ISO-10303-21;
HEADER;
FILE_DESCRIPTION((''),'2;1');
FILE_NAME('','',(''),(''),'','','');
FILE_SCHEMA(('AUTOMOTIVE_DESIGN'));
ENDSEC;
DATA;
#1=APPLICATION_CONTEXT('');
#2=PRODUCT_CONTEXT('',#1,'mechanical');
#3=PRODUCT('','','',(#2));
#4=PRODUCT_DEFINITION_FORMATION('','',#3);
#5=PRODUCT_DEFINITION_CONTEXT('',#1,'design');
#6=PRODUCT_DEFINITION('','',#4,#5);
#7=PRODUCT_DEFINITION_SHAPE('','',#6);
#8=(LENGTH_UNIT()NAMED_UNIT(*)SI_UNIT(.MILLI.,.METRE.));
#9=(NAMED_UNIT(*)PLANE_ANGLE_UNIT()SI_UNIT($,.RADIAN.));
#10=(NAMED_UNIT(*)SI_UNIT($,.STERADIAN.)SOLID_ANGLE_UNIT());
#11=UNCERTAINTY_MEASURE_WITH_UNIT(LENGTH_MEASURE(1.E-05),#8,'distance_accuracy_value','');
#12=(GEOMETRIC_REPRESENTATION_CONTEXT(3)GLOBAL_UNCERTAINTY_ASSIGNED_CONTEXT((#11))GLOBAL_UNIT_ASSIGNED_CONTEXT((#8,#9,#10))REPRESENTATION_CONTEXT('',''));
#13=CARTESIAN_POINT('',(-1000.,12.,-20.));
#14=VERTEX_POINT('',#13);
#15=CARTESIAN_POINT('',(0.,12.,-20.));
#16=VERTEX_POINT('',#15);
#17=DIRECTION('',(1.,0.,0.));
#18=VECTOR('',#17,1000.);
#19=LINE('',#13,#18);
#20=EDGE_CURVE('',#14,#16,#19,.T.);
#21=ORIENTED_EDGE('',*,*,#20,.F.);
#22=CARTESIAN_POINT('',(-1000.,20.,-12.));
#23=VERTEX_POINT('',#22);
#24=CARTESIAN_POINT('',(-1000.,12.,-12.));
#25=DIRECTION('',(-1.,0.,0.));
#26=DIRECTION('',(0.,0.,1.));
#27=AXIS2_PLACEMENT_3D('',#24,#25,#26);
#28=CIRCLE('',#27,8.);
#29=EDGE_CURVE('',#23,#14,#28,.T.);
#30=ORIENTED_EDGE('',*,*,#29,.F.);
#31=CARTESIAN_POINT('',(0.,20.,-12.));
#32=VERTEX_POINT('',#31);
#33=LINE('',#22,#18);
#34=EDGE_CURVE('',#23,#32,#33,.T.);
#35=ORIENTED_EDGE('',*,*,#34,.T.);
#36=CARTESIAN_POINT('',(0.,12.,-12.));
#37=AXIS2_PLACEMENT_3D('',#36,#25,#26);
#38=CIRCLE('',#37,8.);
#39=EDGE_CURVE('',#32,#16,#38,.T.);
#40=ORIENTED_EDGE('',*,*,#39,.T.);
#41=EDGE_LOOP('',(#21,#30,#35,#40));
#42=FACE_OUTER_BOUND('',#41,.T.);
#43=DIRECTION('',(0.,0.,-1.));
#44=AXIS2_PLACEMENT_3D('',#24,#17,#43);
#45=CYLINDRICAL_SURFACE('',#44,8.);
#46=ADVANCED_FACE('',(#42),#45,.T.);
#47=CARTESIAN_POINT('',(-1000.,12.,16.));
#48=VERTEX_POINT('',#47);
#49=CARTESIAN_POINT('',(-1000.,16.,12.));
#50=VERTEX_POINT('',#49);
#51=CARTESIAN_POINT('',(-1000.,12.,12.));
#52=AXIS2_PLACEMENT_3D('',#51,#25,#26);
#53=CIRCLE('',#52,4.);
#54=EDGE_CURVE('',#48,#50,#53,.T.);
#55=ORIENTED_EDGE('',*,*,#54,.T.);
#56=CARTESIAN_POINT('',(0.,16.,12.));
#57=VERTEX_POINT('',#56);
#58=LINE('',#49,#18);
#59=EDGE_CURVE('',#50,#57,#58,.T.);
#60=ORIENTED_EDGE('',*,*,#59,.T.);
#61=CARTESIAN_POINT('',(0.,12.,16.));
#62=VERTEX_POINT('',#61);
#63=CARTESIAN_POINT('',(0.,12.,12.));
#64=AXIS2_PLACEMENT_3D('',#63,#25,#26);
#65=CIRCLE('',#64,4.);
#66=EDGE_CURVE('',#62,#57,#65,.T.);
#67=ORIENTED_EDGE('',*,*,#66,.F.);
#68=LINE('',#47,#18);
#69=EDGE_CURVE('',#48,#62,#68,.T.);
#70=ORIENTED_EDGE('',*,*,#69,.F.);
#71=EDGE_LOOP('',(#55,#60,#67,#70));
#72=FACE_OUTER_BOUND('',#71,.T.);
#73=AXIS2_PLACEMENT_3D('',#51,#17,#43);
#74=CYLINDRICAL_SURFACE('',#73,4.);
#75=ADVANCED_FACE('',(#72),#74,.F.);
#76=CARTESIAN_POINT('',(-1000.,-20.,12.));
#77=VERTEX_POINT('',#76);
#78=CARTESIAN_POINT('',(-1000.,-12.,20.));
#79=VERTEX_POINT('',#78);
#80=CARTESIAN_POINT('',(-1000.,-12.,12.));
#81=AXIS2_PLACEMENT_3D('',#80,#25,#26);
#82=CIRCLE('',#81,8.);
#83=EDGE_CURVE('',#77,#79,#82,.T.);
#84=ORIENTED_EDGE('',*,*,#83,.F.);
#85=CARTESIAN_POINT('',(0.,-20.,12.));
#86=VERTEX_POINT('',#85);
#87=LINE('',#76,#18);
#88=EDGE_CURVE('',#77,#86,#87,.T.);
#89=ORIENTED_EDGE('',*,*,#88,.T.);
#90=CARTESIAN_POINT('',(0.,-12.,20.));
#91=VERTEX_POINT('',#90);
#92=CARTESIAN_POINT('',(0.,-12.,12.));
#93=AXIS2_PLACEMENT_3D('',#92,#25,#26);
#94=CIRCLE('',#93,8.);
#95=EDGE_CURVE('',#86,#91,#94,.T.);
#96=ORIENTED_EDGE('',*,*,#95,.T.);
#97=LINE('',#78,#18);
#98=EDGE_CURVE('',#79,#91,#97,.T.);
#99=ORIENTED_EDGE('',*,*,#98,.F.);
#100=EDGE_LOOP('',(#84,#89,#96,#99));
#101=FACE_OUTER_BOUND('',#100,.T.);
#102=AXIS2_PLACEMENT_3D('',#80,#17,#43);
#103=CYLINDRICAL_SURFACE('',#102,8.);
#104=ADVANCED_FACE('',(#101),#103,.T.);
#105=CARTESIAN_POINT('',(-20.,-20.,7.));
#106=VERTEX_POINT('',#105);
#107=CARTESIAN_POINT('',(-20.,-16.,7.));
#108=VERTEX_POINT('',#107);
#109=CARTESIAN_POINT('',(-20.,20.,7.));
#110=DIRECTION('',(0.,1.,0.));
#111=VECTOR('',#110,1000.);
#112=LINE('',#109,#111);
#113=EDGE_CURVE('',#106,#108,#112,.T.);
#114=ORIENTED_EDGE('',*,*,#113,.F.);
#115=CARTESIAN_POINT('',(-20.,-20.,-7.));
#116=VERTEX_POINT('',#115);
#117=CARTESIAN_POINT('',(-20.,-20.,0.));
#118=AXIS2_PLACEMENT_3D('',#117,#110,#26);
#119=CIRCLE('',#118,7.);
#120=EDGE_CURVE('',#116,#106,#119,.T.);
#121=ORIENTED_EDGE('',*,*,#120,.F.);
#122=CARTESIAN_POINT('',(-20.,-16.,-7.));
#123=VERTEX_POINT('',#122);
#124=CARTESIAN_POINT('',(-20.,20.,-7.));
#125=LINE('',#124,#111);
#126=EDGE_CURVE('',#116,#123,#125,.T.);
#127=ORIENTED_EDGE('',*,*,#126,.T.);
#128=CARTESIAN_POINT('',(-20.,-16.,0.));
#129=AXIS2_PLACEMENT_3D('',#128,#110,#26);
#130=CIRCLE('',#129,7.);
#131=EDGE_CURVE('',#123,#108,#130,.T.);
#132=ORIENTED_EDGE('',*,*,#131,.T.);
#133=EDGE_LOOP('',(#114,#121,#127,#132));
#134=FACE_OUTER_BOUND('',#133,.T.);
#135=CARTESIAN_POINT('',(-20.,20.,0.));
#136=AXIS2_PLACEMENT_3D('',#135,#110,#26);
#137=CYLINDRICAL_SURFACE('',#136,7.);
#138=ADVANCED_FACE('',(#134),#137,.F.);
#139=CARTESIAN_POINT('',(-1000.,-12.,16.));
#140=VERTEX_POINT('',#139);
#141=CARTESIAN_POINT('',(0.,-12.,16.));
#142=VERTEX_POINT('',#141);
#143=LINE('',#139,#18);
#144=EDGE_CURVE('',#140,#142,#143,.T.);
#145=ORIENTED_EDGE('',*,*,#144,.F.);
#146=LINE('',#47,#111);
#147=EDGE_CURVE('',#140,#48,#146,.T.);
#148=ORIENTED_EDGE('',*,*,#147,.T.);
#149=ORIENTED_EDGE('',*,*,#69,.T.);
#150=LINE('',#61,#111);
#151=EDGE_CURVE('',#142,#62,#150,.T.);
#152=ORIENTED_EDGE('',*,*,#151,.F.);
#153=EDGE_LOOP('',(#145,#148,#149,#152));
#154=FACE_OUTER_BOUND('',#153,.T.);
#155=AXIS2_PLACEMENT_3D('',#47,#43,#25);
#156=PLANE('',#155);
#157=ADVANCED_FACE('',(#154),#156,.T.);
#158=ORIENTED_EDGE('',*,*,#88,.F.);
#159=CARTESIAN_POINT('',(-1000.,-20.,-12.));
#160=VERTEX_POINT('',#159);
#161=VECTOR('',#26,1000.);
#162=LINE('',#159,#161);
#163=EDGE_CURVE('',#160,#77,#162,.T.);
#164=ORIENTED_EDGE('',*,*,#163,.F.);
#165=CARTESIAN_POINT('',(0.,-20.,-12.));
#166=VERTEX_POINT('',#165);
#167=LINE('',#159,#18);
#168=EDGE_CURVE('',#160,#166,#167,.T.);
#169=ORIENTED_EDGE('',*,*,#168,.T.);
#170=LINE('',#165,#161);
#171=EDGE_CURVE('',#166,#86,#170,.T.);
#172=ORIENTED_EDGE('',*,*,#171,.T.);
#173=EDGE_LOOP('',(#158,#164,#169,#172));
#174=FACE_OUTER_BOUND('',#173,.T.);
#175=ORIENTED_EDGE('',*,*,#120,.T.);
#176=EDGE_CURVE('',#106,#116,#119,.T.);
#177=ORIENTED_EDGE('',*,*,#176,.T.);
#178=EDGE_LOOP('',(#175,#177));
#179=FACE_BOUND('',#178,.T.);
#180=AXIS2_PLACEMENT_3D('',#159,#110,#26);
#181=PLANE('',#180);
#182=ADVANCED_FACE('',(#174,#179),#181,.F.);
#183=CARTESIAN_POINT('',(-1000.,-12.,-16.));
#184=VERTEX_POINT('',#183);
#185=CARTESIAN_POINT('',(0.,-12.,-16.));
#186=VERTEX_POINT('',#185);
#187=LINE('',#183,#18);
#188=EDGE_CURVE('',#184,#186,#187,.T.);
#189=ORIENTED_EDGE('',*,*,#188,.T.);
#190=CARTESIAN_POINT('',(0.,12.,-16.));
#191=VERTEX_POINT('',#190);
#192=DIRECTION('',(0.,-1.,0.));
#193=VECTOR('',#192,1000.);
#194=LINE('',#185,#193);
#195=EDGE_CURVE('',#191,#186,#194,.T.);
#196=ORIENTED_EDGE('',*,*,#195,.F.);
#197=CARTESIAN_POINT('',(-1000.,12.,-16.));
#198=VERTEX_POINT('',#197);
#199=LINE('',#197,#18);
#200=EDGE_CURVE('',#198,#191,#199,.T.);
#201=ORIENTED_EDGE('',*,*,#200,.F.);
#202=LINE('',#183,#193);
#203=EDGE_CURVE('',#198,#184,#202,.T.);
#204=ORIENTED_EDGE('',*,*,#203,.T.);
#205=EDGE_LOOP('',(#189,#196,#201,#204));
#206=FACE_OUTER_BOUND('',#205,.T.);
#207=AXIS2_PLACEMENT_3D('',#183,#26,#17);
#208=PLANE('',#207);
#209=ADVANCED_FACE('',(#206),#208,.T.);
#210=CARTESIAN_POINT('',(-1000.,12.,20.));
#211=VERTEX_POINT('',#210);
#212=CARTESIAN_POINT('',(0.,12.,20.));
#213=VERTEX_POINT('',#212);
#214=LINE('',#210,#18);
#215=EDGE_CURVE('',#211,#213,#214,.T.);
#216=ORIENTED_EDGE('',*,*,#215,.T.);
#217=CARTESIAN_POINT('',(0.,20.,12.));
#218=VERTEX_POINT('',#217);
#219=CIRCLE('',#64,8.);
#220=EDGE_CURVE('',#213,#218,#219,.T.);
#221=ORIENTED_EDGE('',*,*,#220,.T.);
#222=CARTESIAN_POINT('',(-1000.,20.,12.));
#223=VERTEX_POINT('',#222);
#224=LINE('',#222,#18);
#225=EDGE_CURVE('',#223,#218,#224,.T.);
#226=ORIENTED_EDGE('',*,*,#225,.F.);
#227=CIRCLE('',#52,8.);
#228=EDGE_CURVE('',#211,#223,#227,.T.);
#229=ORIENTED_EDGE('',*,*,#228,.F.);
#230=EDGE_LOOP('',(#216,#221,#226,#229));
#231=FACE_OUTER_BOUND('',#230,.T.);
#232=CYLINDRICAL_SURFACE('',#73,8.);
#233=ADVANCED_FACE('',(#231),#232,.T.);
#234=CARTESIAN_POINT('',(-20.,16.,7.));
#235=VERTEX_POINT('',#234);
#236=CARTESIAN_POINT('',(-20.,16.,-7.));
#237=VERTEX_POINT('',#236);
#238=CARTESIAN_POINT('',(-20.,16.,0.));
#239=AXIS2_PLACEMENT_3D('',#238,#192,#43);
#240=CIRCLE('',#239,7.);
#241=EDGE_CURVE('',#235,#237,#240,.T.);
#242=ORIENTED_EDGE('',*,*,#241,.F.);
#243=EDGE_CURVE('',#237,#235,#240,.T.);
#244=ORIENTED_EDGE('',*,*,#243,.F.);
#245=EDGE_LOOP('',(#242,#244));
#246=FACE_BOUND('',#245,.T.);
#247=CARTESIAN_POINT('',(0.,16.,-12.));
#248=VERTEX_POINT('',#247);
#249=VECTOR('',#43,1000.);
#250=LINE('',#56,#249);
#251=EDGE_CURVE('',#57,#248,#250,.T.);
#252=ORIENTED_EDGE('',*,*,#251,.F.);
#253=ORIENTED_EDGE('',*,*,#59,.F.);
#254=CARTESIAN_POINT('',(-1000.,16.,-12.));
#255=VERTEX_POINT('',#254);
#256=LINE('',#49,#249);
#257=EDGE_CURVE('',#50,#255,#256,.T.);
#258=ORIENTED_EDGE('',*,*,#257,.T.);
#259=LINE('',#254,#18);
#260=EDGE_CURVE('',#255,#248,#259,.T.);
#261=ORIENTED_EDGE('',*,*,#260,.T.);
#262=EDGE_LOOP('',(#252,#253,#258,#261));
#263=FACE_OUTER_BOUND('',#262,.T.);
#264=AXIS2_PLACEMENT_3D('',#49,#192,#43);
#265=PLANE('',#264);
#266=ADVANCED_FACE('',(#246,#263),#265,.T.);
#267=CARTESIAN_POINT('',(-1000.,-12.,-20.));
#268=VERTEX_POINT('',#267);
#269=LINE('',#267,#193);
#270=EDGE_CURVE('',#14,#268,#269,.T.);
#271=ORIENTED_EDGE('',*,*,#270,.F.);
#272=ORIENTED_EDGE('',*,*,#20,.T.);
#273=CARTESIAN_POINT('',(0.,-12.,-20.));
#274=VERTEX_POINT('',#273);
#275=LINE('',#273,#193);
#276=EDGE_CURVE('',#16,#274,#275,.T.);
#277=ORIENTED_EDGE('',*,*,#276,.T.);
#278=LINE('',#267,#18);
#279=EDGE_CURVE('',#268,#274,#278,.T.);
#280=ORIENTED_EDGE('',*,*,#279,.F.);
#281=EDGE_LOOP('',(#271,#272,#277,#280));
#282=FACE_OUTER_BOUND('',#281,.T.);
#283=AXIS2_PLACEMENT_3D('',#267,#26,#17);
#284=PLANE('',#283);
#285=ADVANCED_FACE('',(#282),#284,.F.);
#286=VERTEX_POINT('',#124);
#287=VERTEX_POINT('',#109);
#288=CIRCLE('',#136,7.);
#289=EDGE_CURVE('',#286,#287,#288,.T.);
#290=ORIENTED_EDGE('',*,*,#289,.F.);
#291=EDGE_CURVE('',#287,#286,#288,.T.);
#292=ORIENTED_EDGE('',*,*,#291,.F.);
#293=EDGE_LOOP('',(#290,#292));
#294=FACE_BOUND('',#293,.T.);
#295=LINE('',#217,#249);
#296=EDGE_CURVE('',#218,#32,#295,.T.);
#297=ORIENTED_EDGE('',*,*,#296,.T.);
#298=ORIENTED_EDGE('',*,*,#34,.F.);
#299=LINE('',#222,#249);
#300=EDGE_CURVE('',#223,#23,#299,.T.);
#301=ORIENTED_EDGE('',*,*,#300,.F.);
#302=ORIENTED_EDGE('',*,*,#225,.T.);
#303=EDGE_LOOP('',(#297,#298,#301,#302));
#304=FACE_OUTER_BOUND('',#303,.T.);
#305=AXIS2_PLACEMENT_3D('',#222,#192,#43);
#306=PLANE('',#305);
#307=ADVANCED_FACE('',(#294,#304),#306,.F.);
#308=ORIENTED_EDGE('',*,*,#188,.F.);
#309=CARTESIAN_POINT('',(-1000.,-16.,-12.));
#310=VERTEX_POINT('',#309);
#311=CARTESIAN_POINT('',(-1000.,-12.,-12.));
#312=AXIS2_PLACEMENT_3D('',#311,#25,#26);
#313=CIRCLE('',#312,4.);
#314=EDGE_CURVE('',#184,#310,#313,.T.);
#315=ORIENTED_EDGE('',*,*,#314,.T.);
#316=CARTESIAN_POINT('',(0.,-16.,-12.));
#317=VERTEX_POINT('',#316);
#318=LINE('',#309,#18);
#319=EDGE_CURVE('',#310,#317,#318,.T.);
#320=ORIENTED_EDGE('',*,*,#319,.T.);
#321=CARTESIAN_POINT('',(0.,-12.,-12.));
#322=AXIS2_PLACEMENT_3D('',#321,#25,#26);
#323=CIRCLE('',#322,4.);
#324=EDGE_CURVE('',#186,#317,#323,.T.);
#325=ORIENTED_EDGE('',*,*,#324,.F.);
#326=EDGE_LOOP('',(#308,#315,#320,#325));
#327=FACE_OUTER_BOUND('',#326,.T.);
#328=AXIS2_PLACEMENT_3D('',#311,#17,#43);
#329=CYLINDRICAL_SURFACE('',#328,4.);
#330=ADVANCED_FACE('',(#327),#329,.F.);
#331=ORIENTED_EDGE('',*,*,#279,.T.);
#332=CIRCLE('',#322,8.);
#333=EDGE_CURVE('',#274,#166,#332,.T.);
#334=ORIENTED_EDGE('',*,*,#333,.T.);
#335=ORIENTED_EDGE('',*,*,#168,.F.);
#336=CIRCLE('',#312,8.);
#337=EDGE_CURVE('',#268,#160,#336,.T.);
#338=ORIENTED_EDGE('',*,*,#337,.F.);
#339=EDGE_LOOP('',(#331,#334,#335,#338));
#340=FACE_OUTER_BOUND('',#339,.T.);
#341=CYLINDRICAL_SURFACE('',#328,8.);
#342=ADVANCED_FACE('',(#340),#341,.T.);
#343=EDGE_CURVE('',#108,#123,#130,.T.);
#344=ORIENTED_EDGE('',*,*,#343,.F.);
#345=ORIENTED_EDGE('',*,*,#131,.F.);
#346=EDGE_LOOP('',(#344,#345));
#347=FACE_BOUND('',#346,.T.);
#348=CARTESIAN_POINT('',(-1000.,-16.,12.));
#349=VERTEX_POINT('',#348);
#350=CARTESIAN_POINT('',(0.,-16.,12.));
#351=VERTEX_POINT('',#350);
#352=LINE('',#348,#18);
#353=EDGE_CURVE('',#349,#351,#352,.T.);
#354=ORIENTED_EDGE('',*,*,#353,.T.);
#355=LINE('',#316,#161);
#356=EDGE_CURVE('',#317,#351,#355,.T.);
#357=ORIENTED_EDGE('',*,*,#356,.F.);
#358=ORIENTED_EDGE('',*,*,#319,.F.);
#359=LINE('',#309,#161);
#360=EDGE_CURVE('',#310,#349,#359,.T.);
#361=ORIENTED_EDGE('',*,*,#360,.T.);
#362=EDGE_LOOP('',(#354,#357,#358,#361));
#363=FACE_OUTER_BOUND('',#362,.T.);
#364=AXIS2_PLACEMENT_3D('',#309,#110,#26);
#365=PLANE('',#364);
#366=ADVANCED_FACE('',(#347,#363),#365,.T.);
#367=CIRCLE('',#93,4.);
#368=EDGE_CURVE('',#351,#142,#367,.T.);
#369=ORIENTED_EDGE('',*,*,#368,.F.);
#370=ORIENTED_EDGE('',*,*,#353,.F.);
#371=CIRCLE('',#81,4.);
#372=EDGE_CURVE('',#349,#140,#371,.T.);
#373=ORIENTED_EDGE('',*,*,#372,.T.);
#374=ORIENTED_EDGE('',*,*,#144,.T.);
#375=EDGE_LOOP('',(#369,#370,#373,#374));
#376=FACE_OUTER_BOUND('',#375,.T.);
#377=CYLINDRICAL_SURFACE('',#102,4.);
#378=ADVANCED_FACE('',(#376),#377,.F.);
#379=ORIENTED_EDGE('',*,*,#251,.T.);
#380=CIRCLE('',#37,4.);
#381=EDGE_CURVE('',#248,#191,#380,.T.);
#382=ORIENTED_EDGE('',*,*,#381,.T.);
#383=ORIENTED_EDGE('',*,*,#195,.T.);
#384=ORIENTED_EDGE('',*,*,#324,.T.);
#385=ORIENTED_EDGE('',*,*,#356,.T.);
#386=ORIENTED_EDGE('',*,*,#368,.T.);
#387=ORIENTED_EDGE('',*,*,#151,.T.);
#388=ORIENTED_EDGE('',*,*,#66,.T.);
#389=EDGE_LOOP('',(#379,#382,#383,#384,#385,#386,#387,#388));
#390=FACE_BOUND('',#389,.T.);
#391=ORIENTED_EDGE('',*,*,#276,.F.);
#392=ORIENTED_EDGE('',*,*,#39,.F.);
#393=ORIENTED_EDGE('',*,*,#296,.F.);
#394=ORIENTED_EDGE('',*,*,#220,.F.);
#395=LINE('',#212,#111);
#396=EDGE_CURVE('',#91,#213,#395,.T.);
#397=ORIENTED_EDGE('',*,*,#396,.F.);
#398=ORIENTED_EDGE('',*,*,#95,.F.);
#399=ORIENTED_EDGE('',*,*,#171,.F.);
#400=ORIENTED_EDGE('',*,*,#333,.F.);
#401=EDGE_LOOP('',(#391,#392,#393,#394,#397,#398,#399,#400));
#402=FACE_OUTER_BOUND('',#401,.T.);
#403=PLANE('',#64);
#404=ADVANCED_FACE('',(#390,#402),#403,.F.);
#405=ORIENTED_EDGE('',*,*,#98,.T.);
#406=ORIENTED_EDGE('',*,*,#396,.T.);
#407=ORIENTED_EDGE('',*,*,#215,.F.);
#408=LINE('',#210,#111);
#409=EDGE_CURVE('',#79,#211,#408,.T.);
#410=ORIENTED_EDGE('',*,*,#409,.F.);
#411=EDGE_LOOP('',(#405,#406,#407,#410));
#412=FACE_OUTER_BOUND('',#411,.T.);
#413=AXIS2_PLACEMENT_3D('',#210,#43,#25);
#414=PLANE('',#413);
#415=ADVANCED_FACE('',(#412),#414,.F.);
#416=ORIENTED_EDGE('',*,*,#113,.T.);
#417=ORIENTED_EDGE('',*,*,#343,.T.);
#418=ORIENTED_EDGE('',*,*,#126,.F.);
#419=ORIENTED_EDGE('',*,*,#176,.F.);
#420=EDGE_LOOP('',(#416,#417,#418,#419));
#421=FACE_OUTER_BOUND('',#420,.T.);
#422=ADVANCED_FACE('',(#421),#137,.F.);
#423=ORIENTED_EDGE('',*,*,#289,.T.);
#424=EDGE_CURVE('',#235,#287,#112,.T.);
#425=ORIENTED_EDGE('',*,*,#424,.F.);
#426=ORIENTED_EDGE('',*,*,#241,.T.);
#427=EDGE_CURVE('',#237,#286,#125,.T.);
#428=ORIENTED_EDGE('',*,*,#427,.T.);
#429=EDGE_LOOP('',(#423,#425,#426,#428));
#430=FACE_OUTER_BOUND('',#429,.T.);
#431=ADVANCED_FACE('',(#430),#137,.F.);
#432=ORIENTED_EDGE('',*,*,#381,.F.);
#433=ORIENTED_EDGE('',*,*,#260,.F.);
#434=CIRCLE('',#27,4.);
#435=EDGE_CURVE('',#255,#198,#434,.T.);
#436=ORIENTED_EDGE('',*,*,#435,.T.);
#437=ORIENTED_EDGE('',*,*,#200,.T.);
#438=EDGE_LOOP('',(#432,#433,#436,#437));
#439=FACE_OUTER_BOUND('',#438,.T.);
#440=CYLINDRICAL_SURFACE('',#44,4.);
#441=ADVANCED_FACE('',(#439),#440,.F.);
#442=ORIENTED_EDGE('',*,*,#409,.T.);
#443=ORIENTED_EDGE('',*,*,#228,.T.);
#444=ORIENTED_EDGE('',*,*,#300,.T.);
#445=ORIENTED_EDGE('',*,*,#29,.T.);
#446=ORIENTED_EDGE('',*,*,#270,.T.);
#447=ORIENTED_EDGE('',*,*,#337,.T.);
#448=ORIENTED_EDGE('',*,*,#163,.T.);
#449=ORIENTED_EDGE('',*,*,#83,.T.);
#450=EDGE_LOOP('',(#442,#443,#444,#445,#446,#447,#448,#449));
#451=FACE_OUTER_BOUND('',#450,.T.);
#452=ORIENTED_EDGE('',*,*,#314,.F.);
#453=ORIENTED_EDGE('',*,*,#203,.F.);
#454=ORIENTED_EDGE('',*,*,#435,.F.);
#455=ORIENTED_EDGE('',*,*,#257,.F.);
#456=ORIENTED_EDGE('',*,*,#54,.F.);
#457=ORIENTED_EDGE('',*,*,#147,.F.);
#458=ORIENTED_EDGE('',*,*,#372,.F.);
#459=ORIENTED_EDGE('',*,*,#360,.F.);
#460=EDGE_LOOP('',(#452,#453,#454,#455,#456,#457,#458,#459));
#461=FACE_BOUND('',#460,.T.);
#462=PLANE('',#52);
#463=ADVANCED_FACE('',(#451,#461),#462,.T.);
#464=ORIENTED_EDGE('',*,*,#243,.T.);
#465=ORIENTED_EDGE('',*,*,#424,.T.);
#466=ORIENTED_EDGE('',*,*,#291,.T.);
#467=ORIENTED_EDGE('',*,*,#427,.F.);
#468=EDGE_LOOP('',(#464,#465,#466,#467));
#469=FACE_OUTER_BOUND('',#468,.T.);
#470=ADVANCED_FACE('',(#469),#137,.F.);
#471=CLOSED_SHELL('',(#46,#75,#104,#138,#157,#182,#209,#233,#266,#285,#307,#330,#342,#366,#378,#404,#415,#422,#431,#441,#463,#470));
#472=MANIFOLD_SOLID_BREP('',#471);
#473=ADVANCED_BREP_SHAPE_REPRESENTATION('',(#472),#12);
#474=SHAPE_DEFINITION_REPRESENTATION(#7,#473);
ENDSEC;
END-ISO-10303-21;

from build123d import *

# Parameters (mm, degrees)
GB_6728_1986_040_X_40_X_4_1_DEPTH = 1000
HOLE_WIZARD_M16_1_D               = 14


with BuildPart() as part:
    # Sketch12 → Gb／6728-1986方形空心型钢 040 X 40 X 4(1) (new body)
    with BuildSketch(Plane.ZY):
        with BuildLine():
            Line((-12, -20), (12, -20))
            ThreePointArc((12, -20), (17.656854249, -17.656854249), (20, -12))
            Line((20, -12), (20, 12))
            ThreePointArc((20, 12), (17.656854249, 17.656854249), (12, 20))
            Line((12, 20), (-12, 20))
            ThreePointArc((-12, 20), (-17.656854249, 17.656854249), (-20, 12))
            Line((-20, 12), (-20, -12))
            ThreePointArc((-20, -12), (-17.656854249, -17.656854249), (-12, -20))
        make_face()
        with BuildLine():
            Line((-12, -16), (12, -16))
            ThreePointArc((12, -16), (14.828427125, -14.828427125), (16, -12))
            Line((16, -12), (16, 12))
            ThreePointArc((16, 12), (14.828427125, 14.828427125), (12, 16))
            Line((12, 16), (-12, 16))
            ThreePointArc((-12, 16), (-14.828427125, 14.828427125), (-16, 12))
            Line((-16, 12), (-16, -12))
            ThreePointArc((-16, -12), (-14.828427125, -14.828427125), (-12, -16))
        make_face(mode=Mode.SUBTRACT)
    extrude(amount=GB_6728_1986_040_X_40_X_4_1_DEPTH)

    # M16 螺纹孔1 (through all)
    with Locations(Plane(origin=(0, 20, 0), x_dir=(1, 0, 0), z_dir=(0, 1, 0))):
        with Locations((-20, 0)):
            Hole(HOLE_WIZARD_M16_1_D / 2)


solid = part.part
